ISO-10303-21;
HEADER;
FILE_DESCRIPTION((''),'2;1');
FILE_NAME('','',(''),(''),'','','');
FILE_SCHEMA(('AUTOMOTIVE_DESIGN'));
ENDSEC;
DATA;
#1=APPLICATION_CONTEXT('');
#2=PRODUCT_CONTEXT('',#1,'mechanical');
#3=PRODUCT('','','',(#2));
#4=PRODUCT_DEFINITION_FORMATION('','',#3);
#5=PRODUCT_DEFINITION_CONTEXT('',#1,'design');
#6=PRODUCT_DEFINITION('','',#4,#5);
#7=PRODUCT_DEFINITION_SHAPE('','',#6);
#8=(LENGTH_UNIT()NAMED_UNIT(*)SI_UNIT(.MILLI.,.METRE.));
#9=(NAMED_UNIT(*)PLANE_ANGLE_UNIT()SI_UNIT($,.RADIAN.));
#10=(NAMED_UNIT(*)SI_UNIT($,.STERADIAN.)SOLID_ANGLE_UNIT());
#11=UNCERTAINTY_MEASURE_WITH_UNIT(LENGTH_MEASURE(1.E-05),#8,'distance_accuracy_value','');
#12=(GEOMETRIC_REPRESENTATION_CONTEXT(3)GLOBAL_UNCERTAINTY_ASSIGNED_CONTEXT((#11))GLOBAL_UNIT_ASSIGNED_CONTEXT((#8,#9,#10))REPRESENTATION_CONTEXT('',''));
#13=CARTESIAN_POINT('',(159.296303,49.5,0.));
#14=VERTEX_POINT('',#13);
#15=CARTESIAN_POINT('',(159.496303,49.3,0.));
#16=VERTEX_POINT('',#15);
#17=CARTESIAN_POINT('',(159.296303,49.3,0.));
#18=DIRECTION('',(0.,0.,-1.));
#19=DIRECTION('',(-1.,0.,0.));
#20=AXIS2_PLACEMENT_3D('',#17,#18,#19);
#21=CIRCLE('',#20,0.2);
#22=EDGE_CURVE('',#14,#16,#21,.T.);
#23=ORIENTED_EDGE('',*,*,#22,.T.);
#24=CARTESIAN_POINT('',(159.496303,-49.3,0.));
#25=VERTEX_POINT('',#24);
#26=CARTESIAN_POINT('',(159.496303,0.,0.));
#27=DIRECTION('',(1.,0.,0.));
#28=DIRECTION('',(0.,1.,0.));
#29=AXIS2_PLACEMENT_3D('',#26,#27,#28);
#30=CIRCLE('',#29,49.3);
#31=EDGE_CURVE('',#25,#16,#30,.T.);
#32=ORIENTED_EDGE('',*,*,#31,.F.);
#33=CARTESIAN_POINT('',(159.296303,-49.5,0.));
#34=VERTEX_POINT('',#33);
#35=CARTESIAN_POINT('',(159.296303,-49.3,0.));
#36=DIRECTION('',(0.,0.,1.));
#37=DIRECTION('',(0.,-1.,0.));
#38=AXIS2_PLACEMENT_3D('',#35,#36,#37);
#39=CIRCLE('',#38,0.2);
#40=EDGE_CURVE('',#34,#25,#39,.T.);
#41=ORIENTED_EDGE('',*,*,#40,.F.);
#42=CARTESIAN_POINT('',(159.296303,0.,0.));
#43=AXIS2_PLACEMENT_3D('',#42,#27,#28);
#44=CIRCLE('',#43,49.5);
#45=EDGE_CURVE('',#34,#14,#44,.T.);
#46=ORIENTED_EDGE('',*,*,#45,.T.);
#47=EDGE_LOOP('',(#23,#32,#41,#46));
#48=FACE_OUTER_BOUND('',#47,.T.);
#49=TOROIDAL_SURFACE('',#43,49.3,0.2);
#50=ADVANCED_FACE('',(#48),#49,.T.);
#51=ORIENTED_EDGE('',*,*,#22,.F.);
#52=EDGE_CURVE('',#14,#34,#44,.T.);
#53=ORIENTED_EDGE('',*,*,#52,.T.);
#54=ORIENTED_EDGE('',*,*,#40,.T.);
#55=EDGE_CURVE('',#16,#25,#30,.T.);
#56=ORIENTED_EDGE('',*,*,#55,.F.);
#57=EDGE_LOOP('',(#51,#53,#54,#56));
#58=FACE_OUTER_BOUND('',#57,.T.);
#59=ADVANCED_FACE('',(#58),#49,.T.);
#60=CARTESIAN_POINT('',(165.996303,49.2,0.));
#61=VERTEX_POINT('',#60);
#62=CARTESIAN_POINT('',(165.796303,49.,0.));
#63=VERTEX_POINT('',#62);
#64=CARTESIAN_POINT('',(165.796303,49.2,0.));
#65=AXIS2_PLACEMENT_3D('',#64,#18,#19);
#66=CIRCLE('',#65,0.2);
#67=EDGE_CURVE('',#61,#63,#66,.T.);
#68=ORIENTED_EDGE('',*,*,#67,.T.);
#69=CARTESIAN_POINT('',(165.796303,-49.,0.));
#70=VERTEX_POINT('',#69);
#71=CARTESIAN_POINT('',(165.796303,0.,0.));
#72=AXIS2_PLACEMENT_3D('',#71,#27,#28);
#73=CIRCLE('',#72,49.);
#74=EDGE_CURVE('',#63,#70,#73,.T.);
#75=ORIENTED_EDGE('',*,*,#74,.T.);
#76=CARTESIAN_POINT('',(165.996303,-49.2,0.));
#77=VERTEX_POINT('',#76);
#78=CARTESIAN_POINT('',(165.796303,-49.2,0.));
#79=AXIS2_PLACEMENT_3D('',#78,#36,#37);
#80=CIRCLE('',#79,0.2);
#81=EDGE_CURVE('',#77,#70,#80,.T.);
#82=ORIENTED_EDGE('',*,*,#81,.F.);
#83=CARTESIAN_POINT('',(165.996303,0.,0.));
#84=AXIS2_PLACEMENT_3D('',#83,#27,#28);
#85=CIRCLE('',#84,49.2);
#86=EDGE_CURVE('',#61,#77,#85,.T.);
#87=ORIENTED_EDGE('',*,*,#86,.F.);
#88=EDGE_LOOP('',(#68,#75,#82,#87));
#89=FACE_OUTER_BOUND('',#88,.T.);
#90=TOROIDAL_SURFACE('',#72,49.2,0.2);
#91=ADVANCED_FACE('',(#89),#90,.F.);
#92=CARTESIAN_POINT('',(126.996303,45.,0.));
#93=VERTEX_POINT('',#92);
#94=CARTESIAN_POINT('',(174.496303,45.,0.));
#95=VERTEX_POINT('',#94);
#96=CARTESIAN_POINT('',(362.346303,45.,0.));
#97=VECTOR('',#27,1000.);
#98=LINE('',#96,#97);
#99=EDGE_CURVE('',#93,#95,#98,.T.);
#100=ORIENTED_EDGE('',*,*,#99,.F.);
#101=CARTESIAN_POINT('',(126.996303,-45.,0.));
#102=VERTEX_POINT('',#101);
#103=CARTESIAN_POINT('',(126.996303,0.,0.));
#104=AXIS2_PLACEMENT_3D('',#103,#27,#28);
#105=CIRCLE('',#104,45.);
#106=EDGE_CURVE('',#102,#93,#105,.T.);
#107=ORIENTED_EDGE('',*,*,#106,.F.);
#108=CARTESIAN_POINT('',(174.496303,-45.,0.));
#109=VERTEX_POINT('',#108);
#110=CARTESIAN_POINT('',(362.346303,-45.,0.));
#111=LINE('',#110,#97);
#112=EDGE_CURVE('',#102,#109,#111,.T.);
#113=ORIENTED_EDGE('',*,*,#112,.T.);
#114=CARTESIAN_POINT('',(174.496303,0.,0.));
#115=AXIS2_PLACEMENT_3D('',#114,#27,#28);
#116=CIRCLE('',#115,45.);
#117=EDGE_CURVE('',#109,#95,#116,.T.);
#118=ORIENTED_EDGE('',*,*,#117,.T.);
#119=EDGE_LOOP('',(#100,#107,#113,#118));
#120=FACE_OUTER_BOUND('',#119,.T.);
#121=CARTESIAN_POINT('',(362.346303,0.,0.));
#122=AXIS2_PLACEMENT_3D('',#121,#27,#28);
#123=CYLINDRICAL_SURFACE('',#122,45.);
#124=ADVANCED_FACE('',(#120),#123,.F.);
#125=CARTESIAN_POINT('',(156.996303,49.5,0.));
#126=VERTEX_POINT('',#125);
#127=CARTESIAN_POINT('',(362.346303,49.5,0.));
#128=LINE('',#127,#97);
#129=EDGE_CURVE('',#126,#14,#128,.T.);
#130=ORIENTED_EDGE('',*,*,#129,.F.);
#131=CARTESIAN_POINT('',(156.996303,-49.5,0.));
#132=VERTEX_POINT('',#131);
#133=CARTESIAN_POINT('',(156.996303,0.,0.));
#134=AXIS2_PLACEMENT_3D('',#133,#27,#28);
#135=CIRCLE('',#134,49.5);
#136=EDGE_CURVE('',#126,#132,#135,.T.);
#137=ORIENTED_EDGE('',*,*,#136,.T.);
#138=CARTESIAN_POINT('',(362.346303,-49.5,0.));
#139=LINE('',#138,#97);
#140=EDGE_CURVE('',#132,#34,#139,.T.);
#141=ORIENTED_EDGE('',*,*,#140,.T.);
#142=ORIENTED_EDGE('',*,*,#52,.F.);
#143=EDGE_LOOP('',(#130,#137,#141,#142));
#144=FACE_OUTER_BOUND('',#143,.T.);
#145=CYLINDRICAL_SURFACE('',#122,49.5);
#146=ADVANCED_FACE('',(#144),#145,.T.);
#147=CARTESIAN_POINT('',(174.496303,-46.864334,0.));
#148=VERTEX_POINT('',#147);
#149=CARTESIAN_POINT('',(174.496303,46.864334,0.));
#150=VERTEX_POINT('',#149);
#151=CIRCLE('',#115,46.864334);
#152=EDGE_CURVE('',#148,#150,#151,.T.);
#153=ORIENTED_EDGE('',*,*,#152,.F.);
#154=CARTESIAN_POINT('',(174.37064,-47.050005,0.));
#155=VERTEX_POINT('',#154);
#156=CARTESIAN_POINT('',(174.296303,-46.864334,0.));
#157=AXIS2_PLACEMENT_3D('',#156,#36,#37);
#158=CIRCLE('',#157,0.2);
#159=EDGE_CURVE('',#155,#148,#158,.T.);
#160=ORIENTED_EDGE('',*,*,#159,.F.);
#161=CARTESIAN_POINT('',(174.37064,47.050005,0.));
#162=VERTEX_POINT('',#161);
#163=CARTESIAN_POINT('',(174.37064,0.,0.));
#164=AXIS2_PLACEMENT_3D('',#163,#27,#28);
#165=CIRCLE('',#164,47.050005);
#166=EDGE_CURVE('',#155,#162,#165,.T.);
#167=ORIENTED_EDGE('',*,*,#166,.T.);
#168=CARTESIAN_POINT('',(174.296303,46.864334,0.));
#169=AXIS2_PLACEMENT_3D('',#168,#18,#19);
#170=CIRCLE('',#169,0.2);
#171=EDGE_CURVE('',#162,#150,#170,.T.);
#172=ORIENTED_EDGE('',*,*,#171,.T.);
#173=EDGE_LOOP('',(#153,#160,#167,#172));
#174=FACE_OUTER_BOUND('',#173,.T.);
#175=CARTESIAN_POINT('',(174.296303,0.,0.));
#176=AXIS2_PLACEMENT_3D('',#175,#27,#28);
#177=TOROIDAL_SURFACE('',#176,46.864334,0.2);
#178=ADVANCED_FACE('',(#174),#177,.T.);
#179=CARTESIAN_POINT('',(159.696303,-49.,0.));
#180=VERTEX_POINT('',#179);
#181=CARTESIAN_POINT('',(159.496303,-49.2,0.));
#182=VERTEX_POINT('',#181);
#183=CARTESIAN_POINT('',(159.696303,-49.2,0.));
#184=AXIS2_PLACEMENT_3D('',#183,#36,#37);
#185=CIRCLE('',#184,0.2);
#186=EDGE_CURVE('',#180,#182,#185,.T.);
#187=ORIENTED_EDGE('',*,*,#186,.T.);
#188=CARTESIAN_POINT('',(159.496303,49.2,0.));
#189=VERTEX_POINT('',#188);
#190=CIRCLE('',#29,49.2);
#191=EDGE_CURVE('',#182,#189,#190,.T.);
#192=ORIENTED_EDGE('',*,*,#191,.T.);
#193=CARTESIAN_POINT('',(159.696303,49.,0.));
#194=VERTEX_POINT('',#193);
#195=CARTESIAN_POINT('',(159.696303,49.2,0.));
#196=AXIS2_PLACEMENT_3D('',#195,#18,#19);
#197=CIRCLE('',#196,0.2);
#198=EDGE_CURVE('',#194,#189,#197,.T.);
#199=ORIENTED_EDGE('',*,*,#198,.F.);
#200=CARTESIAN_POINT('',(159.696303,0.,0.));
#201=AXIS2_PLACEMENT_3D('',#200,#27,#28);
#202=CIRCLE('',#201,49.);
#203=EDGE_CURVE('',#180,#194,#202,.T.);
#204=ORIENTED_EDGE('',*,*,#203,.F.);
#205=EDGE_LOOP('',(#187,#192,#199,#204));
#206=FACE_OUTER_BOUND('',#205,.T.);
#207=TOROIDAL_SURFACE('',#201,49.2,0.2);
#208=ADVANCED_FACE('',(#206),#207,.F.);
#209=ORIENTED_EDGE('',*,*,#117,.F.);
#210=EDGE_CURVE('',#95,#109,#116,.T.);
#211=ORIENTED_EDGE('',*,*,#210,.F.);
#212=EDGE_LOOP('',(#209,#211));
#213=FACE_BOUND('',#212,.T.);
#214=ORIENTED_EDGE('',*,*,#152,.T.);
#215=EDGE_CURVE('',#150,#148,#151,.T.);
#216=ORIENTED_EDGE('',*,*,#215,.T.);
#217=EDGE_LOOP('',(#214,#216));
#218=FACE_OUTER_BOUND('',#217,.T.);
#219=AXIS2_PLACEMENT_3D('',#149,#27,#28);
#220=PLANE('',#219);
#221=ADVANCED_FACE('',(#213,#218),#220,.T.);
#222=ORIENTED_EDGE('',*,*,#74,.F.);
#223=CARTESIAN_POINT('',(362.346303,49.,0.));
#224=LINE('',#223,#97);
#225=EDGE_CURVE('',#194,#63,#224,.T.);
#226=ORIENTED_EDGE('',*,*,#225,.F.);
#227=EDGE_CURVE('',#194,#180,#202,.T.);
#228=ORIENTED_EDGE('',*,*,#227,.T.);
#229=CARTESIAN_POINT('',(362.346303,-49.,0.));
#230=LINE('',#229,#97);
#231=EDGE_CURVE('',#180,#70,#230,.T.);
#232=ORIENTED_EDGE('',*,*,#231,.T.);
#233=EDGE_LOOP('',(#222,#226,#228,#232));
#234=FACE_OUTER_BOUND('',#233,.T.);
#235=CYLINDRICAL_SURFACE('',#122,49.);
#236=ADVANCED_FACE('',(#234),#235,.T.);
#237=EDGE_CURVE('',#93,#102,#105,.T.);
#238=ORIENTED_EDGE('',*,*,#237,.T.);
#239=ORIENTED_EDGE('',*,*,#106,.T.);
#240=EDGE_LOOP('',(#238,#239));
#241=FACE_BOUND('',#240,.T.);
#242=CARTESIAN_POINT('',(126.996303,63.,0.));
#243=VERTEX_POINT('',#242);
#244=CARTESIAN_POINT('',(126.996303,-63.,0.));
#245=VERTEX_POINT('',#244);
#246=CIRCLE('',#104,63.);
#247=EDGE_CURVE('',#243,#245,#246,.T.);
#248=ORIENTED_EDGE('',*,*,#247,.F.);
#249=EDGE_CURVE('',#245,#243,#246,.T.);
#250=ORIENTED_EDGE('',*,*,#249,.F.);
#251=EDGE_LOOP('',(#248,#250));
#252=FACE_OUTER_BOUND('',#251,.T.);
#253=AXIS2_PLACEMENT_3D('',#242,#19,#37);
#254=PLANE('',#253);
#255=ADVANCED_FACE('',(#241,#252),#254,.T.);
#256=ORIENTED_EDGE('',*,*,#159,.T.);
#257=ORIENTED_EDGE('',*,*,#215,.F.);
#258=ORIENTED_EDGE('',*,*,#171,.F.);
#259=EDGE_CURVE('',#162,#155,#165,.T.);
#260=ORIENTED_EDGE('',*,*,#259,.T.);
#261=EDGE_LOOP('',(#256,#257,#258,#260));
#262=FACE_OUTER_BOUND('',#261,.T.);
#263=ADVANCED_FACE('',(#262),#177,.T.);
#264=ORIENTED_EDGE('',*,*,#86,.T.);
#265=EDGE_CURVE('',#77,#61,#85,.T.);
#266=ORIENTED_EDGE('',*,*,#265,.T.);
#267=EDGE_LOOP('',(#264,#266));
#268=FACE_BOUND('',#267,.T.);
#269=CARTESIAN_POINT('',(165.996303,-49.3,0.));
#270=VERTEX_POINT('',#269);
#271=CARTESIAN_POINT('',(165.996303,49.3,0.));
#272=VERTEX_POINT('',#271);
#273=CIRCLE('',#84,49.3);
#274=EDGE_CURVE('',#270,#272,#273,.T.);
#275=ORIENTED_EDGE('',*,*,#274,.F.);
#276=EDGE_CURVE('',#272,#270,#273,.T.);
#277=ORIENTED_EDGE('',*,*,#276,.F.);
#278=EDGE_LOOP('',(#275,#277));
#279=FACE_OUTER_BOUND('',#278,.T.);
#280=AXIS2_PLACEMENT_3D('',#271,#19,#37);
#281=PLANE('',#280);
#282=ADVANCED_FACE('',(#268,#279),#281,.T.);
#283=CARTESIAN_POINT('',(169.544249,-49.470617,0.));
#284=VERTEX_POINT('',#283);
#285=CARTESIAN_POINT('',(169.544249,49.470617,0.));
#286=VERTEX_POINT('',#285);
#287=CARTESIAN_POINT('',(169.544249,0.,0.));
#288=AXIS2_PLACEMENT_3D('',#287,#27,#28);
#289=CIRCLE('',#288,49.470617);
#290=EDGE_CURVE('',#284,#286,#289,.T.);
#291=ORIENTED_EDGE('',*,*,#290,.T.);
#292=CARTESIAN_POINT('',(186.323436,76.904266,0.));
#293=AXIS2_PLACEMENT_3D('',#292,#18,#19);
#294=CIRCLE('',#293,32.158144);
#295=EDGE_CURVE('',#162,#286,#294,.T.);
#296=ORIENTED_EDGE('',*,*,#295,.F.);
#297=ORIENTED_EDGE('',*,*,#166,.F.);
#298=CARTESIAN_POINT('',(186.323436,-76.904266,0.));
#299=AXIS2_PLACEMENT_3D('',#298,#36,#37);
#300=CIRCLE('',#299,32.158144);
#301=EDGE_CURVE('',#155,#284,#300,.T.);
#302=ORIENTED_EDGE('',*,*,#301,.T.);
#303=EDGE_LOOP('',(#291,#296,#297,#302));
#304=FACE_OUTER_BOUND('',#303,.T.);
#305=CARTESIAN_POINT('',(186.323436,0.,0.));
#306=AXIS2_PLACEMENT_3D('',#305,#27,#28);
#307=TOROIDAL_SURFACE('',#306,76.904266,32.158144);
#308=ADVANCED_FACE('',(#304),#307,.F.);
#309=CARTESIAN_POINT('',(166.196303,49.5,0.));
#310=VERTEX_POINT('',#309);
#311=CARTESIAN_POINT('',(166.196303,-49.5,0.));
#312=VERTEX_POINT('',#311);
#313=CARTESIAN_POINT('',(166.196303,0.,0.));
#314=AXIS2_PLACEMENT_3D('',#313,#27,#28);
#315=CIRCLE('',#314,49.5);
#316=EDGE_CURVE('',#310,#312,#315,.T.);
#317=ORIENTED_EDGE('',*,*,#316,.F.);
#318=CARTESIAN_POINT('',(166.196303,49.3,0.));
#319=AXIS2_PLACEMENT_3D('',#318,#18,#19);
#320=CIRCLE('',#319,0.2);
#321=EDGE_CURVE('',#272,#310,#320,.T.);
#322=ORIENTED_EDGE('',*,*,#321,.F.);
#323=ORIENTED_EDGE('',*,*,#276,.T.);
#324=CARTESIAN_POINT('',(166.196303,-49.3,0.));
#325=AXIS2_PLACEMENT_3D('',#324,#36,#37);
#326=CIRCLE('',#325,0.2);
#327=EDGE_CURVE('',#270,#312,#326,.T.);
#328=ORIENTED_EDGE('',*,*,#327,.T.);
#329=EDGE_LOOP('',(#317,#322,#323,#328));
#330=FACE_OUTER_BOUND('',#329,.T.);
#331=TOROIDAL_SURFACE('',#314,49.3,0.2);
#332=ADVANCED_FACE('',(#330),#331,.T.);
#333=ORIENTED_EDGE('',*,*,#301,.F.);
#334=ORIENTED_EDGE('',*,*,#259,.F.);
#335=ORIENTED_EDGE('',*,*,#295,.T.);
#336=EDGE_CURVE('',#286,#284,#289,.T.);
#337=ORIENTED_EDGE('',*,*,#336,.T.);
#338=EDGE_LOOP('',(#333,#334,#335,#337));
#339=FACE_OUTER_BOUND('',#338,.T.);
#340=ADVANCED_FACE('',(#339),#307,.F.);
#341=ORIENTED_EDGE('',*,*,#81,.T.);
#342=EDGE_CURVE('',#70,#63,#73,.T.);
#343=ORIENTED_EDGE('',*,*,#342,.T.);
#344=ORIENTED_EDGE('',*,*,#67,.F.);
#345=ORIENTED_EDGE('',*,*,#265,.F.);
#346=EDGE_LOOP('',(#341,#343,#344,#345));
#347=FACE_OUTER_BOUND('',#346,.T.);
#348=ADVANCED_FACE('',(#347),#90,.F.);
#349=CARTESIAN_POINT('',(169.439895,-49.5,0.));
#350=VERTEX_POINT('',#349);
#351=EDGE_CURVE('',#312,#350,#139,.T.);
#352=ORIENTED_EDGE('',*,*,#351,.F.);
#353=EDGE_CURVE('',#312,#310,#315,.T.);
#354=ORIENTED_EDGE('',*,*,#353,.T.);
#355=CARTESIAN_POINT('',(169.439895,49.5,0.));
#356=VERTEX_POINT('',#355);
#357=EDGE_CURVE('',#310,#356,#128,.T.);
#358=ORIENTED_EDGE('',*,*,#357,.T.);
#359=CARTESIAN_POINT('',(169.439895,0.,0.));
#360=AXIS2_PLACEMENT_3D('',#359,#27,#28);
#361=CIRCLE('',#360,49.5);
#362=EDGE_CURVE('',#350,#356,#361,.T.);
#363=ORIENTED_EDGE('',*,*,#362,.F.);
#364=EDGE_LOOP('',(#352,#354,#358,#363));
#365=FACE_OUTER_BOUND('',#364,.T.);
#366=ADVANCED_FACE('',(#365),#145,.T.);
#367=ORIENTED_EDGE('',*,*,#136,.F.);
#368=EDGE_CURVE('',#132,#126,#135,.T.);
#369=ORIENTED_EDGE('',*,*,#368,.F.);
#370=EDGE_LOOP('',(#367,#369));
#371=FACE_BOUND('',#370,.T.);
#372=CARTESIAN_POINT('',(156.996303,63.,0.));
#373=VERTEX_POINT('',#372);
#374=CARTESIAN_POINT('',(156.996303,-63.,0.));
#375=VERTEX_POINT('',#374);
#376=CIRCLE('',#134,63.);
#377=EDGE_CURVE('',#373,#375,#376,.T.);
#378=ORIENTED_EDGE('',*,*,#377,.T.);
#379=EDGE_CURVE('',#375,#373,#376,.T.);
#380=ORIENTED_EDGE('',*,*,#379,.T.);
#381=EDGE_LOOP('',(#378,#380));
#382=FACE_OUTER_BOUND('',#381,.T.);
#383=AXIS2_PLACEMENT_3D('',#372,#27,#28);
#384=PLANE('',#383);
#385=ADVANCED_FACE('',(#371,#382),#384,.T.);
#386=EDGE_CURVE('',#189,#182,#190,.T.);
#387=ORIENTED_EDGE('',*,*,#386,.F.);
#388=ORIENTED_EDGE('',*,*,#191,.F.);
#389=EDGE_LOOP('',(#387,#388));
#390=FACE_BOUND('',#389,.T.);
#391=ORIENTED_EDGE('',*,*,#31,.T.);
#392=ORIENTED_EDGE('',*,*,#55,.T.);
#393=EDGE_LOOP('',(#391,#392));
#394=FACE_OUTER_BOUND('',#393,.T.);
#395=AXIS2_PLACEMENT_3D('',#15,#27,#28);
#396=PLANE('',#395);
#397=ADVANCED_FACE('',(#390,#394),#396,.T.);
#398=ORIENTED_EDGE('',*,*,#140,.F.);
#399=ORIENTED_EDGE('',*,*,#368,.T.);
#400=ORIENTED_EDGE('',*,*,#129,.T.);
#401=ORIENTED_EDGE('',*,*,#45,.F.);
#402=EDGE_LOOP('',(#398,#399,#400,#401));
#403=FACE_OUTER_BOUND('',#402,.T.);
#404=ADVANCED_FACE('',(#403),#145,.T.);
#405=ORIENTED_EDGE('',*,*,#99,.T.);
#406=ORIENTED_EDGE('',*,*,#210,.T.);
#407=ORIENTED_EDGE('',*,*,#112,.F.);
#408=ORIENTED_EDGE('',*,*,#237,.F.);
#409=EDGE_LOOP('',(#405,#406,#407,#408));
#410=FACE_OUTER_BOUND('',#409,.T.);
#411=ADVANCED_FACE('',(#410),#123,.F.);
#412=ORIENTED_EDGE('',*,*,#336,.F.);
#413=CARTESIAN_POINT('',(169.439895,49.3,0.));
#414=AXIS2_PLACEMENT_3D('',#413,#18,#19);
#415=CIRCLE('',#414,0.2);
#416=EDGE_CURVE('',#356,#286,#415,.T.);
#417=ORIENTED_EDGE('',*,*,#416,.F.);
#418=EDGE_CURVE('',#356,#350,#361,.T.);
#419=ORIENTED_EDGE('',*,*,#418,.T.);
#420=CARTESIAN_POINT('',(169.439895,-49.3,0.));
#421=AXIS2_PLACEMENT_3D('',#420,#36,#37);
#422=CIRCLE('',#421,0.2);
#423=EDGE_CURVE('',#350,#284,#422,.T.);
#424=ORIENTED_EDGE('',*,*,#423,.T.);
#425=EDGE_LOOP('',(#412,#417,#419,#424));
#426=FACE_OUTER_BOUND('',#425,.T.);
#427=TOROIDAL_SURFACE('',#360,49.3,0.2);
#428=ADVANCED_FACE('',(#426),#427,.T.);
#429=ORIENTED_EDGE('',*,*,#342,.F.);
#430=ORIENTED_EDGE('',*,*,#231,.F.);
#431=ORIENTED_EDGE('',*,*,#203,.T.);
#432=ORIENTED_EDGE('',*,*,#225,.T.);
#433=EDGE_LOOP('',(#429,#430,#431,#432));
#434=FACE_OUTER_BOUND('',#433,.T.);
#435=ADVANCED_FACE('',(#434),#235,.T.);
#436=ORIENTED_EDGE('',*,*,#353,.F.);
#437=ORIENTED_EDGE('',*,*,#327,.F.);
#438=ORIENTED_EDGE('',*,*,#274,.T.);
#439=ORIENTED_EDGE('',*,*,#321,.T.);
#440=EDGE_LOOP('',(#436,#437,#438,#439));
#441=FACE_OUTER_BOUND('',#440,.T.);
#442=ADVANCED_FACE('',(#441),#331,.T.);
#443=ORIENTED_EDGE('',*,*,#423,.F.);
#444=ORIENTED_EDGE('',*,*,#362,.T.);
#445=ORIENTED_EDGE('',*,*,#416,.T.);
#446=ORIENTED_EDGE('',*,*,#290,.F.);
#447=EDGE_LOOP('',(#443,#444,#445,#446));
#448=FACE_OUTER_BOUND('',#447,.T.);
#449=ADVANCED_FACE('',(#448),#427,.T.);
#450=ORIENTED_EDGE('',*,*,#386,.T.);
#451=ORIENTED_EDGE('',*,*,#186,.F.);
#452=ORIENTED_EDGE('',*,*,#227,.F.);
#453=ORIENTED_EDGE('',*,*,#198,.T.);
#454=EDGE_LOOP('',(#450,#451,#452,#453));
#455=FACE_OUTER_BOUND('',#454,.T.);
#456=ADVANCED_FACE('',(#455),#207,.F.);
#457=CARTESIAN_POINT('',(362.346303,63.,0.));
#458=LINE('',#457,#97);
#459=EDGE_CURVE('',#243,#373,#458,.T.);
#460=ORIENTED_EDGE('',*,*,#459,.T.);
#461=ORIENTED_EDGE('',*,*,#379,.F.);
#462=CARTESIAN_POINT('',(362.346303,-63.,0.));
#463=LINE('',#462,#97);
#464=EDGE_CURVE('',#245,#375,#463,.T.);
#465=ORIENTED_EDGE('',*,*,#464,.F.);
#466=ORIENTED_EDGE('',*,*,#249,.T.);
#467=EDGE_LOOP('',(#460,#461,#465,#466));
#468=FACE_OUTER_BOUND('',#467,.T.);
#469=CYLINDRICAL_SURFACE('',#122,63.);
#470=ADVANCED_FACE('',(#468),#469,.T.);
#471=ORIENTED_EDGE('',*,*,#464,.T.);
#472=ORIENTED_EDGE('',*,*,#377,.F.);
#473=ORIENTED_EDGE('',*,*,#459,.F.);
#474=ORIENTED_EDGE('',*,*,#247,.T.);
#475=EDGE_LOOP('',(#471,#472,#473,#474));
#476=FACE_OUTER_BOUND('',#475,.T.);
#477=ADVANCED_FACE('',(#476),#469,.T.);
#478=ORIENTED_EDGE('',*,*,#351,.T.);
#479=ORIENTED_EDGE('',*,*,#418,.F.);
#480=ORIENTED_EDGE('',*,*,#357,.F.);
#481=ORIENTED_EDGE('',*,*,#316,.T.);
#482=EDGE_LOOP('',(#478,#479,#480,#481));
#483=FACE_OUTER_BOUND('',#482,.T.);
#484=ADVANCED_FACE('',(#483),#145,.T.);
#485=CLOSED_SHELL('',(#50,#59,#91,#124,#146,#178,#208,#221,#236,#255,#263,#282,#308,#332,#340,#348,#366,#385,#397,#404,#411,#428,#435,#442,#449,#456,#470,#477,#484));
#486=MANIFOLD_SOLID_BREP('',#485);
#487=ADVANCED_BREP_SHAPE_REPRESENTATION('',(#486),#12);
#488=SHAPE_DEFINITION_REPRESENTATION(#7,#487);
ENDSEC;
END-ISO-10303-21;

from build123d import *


with BuildPart() as part:
    # Sketch2 → Revolve1 (revolve)
    with BuildSketch(Plane.XY):
        with BuildLine():
            Line((169.439894657, 49.5), (166.196302637, 49.5))
            ThreePointArc((166.196302637, 49.5), (166.054881281, 49.441421356), (165.996302637, 49.3))
            Line((165.996302637, 49.3), (165.996302637, 49.2))
            ThreePointArc((165.996302637, 49.2), (165.937723993, 49.058578644), (165.796302637, 49))
            Line((165.796302637, 49), (159.696302637, 49))
            ThreePointArc((159.696302637, 49), (159.554881281, 49.058578644), (159.496302637, 49.2))
            Line((159.496302637, 49.2), (159.496302637, 49.3))
            ThreePointArc((159.496302637, 49.3), (159.437723993, 49.441421356), (159.296302637, 49.5))
            Line((159.296302637, 49.5), (156.996302637, 49.5))
            Line((156.996302637, 49.5), (156.996302637, 63))
            Line((156.996302637, 63), (126.996302637, 63))
            Line((126.996302637, 63), (126.996302637, 45))
            Line((126.996302637, 45), (174.496302637, 45))
            Line((174.496302637, 45), (174.496302637, 46.864333756))
            ThreePointArc((174.496302637, 46.864333756), (174.461934034, 46.976432999), (174.370640233, 47.050005299))
            ThreePointArc((174.370640233, 47.050005299), (171.90655177, 48.158837504), (169.544248857, 49.470617118))
            ThreePointArc((169.544248857, 49.470617118), (169.494100636, 49.492514186), (169.439894657, 49.5))
        make_face()
    revolve(axis=Axis((362.346302637, 0, 0), (-1, 0, 0)))


solid = part.part
